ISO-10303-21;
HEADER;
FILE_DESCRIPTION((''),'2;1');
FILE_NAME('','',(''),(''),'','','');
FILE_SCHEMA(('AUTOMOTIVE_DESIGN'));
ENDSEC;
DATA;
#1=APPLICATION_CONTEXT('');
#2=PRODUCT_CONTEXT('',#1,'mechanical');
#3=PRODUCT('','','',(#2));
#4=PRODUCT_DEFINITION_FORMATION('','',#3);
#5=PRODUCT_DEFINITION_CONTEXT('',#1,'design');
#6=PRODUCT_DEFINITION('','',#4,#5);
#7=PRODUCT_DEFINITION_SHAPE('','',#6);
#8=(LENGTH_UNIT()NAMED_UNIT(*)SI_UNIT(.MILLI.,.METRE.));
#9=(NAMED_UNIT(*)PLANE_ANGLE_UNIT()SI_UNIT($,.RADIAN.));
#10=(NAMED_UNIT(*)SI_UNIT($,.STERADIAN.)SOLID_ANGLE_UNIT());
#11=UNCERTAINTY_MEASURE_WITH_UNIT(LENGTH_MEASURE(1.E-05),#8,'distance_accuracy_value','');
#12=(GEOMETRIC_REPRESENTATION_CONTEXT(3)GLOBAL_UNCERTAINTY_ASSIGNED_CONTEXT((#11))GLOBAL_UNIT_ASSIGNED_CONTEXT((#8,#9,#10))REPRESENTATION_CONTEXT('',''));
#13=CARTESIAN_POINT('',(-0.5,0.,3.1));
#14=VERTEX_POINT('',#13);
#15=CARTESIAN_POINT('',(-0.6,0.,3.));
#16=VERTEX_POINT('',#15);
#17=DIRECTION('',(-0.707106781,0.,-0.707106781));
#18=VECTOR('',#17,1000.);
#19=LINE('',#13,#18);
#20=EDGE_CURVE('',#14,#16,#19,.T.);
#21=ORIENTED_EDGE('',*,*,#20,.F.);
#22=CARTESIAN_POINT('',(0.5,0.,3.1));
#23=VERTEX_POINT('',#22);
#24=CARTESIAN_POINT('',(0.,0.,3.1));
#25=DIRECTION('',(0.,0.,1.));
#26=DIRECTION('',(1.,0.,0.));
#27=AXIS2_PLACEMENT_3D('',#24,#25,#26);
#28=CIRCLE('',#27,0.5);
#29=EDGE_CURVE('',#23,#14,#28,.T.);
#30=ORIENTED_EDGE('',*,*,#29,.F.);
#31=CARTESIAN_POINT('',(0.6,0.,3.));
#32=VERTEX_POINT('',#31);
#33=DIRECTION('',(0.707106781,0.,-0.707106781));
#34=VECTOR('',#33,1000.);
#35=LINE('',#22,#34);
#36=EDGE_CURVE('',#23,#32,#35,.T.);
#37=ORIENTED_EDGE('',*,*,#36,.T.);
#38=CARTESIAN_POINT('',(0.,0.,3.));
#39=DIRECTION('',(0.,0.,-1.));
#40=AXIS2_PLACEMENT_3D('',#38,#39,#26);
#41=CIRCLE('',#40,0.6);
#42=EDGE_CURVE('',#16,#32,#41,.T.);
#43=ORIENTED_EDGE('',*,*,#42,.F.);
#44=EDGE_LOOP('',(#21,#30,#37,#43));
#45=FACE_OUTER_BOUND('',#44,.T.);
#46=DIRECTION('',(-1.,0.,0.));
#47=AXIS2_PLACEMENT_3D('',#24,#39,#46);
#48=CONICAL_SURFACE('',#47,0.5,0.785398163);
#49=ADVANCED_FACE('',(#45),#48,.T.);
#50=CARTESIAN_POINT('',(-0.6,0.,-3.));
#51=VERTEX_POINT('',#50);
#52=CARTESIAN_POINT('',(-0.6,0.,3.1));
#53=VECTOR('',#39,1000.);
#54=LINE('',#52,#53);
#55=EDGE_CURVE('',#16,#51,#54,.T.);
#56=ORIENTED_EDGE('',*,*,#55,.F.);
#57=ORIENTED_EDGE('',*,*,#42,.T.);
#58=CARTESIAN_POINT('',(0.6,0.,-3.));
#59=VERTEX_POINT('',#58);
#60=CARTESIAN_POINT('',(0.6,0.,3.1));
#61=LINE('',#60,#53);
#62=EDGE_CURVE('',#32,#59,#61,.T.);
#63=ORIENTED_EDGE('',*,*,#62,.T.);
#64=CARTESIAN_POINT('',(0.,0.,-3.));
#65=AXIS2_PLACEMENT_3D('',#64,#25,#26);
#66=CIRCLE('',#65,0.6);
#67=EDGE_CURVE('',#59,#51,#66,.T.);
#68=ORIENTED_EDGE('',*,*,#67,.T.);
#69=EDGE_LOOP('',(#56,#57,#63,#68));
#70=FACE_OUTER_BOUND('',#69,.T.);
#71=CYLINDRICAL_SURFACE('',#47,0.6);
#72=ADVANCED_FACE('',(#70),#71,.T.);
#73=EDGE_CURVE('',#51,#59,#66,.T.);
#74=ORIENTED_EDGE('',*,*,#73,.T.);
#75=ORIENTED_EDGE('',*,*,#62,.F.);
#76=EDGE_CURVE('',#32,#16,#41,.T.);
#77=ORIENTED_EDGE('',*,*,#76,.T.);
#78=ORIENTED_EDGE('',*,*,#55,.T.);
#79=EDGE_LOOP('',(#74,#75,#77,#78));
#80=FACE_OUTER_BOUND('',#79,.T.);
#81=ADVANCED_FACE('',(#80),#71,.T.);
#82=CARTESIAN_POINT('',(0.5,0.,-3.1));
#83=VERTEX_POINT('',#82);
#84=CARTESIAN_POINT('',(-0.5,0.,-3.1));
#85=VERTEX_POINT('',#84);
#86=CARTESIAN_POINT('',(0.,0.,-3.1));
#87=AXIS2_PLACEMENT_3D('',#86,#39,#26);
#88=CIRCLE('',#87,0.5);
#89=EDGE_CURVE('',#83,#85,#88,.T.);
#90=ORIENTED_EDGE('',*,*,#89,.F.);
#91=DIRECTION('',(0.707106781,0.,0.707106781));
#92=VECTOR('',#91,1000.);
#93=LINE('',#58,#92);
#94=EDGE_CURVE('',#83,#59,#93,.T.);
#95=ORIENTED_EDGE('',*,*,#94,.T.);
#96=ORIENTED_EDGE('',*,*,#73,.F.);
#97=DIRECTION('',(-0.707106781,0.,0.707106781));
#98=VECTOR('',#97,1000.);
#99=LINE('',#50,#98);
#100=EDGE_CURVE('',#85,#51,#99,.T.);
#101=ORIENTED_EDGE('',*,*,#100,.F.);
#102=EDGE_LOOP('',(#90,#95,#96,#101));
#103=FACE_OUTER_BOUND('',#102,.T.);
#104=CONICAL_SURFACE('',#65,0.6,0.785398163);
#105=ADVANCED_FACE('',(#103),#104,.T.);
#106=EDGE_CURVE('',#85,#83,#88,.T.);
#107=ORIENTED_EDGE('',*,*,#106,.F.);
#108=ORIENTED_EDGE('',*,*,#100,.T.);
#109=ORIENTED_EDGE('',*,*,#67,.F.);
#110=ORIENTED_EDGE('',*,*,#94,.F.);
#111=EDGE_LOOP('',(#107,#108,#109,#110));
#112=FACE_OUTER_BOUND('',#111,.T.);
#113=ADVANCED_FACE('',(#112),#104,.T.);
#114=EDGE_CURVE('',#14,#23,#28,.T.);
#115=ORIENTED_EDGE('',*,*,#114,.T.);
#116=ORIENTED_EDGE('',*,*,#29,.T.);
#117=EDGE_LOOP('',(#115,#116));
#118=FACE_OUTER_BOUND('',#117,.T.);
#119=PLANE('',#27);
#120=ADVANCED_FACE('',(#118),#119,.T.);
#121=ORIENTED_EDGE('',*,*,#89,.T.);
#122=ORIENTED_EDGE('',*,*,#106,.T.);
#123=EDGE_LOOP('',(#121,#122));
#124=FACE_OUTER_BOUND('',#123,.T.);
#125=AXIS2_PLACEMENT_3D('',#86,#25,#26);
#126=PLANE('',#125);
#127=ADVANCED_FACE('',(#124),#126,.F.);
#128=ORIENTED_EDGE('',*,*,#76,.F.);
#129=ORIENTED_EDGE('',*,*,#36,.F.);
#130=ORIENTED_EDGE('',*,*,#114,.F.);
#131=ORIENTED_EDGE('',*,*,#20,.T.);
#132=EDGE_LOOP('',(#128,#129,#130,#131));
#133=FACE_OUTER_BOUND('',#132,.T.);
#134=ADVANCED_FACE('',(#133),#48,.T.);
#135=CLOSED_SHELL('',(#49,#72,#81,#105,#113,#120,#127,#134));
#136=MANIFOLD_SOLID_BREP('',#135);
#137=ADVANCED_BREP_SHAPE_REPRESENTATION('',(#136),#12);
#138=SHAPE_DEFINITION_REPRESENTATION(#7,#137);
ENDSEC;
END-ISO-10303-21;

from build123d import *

# Parameters (mm, degrees)
SKETCH1_R           = 0.6
BOSS_EXTRUDE1_DEPTH = 3.1
CHAMFER1_SIZE       = 0.1


with BuildPart() as part:
    # Sketch1 → Boss-Extrude1 (new, symmetric)
    with BuildSketch(Plane.XY):
        Circle(SKETCH1_R)
    extrude(amount=BOSS_EXTRUDE1_DEPTH, both=True)

    # Chamfer1
    chamfer1_edges = [part.edges().sort_by_distance(p)[0] for p in [
        (-0.6, 0, -3.1),
        (-0.6, 0, 3.1),
    ]]
    chamfer(chamfer1_edges, length=CHAMFER1_SIZE)


solid = part.part
